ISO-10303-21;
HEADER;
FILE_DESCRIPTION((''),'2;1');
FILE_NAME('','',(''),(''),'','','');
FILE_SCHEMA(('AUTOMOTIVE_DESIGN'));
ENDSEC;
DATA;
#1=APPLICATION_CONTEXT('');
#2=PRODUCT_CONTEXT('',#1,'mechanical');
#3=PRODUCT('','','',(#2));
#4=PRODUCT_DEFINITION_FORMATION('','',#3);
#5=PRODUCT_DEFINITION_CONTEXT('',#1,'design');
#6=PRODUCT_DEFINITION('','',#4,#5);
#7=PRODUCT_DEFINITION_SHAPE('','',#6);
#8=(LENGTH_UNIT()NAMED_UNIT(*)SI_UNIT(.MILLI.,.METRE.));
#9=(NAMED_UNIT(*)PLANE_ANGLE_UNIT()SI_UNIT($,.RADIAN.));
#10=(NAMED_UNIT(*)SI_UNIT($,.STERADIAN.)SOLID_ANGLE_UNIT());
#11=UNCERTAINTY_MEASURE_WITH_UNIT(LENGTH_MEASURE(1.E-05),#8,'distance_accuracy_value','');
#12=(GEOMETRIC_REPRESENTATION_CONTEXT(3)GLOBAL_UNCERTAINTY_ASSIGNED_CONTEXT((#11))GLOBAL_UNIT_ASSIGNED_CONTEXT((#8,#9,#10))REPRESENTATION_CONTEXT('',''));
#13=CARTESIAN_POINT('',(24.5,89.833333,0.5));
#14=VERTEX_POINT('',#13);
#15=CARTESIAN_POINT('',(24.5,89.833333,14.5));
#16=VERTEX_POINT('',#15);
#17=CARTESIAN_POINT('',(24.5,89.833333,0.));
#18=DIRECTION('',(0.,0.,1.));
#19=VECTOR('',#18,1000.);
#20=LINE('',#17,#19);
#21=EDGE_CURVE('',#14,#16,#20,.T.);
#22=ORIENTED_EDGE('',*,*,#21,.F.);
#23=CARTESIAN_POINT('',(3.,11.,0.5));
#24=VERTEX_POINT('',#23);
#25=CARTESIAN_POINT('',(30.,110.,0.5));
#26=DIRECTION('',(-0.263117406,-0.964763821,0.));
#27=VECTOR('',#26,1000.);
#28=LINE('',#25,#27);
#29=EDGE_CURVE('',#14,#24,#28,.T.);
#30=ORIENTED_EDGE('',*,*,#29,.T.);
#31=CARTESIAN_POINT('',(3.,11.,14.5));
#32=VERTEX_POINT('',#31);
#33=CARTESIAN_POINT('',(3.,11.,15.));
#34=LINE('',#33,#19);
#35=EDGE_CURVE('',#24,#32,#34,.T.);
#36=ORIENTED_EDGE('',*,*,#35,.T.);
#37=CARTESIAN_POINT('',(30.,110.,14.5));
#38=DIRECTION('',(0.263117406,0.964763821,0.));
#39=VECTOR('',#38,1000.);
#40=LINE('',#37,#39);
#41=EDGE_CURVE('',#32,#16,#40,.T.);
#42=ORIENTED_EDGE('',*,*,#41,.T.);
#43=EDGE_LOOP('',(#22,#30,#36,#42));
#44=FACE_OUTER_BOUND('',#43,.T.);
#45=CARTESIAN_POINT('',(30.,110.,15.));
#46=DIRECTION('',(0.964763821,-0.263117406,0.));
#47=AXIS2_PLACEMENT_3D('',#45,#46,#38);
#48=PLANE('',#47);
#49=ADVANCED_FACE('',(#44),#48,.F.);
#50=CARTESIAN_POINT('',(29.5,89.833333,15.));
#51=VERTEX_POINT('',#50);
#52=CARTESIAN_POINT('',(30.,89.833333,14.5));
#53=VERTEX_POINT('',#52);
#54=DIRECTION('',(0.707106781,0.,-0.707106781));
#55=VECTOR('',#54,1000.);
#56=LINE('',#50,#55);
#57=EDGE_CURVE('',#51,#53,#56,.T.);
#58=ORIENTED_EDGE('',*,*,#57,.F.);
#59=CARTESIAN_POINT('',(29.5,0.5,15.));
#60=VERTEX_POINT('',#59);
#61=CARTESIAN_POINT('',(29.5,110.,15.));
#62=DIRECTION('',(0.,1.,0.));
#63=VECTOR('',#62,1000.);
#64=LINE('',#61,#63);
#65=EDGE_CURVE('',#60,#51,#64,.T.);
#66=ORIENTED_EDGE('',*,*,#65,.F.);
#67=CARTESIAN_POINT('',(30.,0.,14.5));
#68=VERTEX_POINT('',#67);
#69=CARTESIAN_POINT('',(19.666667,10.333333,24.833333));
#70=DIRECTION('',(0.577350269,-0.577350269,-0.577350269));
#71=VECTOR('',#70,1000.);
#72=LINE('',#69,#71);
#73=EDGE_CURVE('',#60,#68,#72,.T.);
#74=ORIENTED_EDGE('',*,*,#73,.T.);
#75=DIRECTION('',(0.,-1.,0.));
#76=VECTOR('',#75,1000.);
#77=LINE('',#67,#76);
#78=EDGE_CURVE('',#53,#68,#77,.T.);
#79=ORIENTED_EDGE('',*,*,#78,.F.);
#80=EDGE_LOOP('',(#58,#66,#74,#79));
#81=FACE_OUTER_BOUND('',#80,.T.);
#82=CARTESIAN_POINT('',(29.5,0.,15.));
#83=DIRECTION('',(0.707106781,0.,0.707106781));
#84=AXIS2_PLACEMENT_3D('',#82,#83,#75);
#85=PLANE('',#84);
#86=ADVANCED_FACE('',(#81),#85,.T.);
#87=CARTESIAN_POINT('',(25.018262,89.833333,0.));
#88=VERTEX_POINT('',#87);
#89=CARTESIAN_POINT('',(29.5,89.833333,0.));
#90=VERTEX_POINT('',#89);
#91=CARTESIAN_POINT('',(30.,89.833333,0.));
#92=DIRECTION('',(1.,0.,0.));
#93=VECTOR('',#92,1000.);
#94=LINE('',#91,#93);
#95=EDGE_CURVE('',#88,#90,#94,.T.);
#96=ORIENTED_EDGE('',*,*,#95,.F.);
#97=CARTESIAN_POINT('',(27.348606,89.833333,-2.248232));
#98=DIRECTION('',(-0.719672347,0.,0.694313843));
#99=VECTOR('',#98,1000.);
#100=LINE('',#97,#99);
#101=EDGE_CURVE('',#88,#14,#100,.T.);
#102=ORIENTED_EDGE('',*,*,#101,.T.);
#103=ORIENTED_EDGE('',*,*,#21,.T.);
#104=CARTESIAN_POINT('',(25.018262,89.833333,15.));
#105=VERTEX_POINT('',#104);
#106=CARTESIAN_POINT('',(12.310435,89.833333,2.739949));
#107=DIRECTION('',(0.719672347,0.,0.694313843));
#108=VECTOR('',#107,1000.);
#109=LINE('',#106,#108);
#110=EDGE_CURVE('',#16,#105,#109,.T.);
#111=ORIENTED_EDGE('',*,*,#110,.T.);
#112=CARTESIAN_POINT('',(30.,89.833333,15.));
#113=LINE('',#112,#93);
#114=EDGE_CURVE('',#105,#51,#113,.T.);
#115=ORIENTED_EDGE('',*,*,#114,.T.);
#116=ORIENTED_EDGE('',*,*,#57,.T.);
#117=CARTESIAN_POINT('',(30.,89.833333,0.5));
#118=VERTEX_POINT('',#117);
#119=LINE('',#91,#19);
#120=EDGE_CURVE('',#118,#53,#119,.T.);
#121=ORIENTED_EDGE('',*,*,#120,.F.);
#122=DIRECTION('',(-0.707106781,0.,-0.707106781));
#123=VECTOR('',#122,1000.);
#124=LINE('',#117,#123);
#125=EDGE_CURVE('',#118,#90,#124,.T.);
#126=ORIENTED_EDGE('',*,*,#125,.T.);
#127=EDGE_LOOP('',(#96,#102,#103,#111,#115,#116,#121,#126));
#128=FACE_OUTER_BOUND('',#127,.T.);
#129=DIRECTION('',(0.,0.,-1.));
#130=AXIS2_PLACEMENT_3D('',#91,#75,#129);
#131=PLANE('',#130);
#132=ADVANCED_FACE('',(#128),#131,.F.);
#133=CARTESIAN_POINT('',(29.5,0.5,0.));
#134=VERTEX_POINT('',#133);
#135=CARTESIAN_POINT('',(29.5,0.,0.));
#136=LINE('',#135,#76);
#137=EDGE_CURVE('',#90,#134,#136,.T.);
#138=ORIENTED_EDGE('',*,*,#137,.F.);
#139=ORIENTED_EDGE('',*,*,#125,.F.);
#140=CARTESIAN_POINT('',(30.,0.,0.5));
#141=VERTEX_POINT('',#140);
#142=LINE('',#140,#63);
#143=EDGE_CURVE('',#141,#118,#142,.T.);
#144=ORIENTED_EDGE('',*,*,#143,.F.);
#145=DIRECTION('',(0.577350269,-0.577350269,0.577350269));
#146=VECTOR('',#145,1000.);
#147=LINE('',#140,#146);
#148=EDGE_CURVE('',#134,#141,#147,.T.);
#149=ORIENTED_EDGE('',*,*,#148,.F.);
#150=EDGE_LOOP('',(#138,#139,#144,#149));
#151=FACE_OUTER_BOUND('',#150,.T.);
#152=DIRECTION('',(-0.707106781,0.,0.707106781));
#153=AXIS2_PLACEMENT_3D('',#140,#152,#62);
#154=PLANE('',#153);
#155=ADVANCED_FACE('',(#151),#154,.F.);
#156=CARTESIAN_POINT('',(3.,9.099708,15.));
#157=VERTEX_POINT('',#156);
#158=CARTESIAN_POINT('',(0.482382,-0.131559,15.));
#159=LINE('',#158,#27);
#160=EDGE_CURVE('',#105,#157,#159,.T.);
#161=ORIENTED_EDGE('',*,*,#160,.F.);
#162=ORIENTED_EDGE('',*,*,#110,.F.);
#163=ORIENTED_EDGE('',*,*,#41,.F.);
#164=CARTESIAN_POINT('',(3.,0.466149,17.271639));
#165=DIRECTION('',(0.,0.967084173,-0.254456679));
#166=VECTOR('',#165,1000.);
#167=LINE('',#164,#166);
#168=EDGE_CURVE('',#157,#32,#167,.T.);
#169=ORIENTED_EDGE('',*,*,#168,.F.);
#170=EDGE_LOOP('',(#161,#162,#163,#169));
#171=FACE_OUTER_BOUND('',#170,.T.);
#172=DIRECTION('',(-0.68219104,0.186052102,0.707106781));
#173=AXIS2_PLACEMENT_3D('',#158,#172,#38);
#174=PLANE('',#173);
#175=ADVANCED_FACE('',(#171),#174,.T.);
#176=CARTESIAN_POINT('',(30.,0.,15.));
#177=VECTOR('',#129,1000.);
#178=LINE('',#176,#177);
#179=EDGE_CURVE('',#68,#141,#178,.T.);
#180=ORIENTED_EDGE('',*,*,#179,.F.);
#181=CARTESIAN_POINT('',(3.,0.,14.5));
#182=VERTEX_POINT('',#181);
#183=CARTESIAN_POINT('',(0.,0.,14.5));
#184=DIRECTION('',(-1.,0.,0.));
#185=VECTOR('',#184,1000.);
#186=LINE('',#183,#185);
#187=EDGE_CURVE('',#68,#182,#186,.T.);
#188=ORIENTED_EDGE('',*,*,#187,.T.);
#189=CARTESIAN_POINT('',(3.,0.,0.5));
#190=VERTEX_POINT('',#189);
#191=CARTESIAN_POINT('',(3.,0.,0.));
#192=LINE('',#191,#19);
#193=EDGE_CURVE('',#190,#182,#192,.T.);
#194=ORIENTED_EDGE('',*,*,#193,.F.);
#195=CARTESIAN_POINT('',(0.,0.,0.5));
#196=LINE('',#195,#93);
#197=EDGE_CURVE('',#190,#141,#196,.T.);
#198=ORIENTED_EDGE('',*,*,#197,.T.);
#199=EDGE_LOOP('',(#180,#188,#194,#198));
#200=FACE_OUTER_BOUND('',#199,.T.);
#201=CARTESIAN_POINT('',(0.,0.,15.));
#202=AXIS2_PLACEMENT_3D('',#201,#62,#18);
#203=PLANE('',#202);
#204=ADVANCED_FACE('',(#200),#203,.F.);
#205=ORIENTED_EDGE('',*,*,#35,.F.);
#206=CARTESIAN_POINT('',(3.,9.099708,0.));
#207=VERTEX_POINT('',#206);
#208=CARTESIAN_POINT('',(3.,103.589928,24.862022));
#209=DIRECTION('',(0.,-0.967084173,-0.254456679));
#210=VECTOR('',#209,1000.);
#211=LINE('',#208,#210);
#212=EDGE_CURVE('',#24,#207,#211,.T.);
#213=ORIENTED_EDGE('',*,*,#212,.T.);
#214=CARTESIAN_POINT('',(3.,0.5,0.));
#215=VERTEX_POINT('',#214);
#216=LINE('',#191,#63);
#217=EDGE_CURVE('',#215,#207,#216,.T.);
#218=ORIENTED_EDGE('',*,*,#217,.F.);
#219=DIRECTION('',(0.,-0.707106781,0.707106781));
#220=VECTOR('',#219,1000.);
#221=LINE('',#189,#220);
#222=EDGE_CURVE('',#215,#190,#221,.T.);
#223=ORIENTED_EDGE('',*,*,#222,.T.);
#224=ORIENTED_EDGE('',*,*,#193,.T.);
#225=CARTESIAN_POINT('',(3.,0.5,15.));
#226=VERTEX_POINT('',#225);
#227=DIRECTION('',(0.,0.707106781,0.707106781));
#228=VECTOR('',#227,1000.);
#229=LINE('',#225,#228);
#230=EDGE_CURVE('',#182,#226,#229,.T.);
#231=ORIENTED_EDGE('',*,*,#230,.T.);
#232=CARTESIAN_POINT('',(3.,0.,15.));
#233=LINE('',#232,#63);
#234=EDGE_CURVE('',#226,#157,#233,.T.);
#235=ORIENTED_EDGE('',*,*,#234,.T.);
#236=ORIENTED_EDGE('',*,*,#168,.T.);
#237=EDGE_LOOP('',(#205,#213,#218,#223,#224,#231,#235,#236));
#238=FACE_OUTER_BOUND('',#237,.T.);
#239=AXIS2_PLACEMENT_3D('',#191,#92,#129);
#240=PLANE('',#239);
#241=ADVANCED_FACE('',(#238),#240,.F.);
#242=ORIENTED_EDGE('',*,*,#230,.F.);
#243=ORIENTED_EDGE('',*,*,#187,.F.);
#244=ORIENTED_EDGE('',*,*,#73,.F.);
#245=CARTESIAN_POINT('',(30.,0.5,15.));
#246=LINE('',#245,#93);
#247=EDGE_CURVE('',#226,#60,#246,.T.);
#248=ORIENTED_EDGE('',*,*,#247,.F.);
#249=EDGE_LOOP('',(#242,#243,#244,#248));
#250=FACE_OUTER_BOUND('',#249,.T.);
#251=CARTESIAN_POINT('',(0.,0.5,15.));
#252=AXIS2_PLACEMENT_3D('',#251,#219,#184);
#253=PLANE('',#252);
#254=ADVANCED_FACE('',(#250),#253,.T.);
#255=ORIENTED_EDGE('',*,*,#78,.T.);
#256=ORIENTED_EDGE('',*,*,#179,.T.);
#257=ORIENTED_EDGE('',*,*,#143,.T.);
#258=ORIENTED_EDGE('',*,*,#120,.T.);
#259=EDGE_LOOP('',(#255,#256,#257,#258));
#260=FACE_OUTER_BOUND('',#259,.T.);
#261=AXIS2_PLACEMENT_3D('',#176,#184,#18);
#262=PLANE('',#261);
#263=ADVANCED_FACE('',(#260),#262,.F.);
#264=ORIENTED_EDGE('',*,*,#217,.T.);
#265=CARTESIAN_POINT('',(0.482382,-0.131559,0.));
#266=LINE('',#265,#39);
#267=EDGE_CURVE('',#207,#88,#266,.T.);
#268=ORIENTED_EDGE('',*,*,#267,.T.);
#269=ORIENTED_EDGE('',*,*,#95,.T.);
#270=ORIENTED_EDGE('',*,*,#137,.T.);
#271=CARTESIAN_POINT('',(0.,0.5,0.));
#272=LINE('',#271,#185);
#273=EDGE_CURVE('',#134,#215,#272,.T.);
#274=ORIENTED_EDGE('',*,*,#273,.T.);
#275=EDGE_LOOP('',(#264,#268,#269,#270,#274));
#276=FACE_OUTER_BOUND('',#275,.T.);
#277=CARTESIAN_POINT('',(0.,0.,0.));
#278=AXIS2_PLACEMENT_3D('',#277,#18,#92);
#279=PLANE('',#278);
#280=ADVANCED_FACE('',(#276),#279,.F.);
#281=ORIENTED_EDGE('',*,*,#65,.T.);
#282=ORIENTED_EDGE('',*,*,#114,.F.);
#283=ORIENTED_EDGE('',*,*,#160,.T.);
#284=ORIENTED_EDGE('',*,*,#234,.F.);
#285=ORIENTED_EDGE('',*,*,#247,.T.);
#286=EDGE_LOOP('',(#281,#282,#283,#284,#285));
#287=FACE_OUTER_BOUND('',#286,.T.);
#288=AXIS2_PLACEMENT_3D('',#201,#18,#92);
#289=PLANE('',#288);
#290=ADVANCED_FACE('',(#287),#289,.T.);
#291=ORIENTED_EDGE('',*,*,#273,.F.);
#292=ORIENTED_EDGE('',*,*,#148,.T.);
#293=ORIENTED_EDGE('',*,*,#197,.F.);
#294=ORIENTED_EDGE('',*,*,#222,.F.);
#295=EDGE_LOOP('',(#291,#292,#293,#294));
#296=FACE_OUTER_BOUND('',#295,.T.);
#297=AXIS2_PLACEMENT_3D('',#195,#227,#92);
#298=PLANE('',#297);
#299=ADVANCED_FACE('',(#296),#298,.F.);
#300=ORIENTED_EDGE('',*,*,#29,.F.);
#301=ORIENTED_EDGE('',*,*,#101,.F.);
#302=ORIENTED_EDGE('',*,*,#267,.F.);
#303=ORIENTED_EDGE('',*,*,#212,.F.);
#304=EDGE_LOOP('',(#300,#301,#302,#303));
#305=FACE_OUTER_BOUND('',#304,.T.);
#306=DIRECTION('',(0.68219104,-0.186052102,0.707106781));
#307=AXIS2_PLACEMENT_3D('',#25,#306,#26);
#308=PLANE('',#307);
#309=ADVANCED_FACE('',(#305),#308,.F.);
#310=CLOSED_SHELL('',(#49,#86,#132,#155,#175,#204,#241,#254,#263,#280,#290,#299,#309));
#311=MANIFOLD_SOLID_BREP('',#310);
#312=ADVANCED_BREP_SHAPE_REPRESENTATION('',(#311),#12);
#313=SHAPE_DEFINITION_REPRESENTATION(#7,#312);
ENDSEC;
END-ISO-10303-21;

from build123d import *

# Parameters (mm, degrees)
EXTRUDE_1_DEPTH     = 15
CHAMFER_1_SIZE      = 0.5
SKETCH_7_W          = 5.5
SKETCH_7_H          = 20.166666667
SKETCH_7_W_2        = 3
SKETCH_7_H_2        = 20
CUT_EXTRUDE_1_DEPTH = 116


with BuildPart() as part:
    # 草图1 → 凸台-拉伸1 (new body)
    with BuildSketch(Plane.XY):
        Polygon((0, 0), (30, 0), (30, 110), align=None)
    extrude(amount=EXTRUDE_1_DEPTH)

    # 倒角1
    chamfer_1_edges = [part.edges().sort_by_distance(p)[0] for p in [
        (30, 55, 15),
        (30, 55, 0),
        (15, 55, 15),
        (15, 0, 0),
        (15, 55, 0),
        (15, 0, 15),
    ]]
    chamfer(chamfer_1_edges, length=CHAMFER_1_SIZE)

    # 草图7 → 切除-拉伸1 (cut, through all)
    with BuildSketch(Plane.XY.offset(15)):
        with Locations((27.25, 99.916666666)):
            Rectangle(SKETCH_7_W, SKETCH_7_H)
        with Locations((1.5, 10)):
            Rectangle(SKETCH_7_W_2, SKETCH_7_H_2)
    extrude(amount=-CUT_EXTRUDE_1_DEPTH, mode=Mode.SUBTRACT)


solid = part.part
